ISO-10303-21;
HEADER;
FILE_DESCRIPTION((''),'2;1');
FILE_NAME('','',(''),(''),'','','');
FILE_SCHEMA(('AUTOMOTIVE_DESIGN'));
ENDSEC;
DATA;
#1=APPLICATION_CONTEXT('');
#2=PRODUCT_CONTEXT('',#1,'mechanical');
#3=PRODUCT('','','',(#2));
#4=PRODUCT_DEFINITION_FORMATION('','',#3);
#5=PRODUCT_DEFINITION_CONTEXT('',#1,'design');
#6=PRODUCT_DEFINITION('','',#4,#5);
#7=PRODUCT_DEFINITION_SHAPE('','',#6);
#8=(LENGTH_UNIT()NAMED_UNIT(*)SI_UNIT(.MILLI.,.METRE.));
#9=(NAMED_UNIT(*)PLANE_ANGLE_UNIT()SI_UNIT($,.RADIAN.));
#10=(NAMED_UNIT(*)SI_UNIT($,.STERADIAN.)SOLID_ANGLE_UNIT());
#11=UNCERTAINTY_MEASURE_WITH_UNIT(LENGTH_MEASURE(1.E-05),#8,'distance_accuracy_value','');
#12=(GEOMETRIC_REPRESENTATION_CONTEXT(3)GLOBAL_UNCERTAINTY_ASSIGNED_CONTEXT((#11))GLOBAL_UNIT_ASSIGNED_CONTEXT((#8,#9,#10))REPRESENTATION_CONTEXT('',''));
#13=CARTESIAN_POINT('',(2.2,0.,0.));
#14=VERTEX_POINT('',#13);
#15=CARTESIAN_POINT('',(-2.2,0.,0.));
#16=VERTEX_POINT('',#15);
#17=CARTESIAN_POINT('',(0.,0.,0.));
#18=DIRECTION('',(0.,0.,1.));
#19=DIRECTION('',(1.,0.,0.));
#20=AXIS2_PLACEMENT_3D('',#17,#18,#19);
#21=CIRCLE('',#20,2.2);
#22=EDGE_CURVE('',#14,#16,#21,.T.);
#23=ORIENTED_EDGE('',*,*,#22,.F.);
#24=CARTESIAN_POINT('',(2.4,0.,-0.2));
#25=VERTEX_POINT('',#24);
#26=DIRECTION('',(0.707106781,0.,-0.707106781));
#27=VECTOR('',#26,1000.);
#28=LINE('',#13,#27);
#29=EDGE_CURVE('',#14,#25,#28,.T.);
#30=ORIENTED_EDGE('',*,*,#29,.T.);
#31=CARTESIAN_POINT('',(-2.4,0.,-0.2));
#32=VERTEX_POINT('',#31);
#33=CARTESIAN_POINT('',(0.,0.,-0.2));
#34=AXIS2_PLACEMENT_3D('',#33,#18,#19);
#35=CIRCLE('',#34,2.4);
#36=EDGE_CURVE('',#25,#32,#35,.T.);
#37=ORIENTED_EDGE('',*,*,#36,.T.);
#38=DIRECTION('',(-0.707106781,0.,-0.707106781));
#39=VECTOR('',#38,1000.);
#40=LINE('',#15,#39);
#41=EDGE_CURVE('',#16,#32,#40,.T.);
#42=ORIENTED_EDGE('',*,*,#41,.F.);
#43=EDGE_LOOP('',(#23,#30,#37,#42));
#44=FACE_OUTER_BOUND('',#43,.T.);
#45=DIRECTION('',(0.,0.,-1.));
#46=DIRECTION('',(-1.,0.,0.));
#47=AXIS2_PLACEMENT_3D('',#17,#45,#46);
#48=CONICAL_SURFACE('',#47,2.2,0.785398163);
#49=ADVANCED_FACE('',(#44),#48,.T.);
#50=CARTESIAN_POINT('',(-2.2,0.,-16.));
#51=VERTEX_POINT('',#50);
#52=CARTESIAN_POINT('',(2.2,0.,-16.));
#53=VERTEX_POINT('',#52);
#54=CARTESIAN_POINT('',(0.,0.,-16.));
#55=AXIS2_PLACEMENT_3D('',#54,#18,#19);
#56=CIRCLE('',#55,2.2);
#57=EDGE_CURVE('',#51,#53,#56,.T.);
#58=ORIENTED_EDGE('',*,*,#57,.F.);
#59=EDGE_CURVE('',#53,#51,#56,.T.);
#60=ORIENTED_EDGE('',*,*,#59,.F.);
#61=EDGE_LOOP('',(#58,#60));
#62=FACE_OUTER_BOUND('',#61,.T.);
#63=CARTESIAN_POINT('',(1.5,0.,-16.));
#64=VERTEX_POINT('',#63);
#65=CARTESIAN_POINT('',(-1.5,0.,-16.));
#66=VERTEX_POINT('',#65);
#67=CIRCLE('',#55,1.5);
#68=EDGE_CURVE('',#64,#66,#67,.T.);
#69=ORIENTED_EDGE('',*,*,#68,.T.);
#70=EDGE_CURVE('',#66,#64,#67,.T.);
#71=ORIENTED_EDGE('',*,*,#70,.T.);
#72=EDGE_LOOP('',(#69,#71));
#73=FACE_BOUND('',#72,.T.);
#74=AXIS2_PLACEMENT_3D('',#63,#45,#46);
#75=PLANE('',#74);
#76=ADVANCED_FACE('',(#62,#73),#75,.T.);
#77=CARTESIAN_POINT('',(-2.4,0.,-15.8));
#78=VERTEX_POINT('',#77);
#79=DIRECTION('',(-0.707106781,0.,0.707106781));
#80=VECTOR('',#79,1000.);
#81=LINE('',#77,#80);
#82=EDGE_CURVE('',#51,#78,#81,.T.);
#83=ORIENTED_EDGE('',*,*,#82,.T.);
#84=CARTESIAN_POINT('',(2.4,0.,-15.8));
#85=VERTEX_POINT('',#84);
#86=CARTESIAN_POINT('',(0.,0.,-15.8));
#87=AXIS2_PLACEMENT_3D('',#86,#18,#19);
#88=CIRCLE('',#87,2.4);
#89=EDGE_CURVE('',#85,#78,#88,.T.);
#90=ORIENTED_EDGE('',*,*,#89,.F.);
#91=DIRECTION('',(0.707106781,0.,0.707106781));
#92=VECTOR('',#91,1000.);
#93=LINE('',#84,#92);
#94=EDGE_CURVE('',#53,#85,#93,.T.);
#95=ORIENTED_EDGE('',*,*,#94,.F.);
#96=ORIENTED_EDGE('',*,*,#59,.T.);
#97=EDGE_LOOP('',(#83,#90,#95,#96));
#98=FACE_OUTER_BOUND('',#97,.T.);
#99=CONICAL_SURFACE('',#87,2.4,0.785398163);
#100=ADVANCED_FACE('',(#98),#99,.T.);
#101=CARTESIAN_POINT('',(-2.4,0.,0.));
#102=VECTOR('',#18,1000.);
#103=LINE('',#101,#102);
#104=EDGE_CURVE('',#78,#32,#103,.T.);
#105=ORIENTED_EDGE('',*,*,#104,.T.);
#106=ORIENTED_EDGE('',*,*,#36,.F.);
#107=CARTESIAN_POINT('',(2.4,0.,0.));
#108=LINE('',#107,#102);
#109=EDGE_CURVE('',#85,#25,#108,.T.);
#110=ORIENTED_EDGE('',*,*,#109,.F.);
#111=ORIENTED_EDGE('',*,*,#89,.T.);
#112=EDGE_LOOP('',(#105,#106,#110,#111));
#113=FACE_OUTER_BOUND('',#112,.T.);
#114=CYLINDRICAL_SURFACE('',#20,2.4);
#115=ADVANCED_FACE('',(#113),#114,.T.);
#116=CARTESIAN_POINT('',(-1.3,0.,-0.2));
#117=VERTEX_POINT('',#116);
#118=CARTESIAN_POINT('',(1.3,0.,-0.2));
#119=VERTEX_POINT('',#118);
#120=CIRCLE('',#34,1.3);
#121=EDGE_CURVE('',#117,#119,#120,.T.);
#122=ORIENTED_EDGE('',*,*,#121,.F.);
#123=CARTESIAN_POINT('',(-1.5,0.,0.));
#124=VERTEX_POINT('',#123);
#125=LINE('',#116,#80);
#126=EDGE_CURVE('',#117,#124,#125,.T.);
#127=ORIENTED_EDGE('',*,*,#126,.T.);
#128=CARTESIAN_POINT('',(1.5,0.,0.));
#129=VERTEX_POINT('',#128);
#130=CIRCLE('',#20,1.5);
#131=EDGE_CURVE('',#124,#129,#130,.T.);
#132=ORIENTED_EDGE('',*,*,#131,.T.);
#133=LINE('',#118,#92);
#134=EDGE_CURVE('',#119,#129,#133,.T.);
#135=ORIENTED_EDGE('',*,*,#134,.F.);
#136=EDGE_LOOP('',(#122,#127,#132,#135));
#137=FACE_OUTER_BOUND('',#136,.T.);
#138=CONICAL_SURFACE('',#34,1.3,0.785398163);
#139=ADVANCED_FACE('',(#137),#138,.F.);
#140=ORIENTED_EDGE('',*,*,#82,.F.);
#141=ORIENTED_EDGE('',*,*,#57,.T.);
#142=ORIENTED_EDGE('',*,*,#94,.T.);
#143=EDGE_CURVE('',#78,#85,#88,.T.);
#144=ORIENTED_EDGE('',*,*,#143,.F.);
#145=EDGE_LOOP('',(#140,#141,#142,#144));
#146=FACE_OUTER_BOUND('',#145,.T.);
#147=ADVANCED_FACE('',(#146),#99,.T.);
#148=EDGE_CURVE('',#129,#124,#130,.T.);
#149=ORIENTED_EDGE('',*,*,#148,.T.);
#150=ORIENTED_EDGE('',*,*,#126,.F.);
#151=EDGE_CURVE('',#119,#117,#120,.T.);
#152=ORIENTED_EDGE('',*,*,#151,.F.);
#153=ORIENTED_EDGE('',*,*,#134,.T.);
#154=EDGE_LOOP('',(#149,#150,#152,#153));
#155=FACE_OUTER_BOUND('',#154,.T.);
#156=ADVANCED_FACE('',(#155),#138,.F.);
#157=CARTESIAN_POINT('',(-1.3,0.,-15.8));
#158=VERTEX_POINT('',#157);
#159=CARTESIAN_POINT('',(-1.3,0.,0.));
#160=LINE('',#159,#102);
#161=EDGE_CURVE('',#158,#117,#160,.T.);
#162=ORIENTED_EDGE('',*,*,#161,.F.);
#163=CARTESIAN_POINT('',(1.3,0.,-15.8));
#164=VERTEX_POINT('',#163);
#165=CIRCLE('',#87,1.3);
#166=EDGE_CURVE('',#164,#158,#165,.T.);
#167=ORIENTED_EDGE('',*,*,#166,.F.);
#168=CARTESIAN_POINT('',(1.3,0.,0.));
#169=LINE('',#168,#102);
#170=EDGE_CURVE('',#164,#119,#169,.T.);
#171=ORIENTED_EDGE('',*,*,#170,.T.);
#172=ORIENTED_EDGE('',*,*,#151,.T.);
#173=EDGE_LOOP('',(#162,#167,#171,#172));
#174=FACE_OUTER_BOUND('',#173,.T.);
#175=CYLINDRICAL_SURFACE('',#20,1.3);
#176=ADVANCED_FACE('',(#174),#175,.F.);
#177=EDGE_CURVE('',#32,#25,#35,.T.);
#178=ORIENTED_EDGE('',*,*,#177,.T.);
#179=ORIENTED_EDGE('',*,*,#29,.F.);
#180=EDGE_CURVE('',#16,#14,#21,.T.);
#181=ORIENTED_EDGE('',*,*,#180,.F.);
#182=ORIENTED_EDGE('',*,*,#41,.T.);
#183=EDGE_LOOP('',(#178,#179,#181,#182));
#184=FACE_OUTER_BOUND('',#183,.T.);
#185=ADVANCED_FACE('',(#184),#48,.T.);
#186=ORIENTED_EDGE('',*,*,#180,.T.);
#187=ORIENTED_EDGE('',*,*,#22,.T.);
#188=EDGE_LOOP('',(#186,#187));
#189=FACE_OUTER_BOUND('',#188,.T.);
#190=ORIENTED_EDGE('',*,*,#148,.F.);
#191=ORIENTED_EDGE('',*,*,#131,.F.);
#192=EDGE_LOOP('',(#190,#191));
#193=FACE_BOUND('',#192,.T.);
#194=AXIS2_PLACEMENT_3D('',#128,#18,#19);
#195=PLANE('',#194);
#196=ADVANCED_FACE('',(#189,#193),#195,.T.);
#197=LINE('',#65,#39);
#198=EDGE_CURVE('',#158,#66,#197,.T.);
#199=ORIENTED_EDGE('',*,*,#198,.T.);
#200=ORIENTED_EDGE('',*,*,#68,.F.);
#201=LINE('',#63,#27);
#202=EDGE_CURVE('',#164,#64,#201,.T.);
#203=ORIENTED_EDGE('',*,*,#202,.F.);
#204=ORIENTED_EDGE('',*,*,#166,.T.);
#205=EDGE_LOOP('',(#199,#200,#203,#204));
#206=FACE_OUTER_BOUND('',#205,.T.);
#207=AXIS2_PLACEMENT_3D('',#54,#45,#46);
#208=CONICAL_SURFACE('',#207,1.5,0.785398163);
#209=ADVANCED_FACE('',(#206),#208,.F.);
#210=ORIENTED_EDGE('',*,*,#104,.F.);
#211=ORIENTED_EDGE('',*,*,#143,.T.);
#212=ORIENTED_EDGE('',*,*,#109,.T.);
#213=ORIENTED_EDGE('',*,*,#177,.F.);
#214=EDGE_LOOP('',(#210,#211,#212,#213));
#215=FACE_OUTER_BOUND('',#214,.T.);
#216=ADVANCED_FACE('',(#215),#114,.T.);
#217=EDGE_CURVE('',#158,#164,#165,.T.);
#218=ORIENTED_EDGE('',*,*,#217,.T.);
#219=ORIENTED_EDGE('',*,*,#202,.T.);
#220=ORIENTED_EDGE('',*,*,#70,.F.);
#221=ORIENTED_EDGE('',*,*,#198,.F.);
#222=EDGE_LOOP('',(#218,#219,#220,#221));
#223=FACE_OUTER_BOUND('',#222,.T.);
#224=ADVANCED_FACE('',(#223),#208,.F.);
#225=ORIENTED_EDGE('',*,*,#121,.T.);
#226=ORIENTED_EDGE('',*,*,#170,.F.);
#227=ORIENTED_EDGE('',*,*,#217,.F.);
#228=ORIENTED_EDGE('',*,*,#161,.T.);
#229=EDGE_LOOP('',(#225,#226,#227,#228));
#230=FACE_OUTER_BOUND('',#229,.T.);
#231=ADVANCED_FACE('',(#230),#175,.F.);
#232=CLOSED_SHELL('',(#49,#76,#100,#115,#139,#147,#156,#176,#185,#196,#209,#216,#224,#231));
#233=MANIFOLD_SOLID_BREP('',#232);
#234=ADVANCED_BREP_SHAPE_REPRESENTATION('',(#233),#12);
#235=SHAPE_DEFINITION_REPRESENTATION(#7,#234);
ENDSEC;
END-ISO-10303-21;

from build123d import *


with BuildPart() as part:
    # Sketch2 → Revolve1 (revolve)
    with BuildSketch(Plane(origin=(0, 0, 0), x_dir=(1, 0, 0), z_dir=(0, 1, 0))):
        Polygon((1.5, 0), (2.2, 0), (2.4, 0.2), (2.4, 15.8), (2.2, 16), (1.5, 16), (1.3, 15.8), (1.3, 0.2), align=None)
    revolve(axis=Axis((0, 0, 0), (0, 0, -1)))


solid = part.part
